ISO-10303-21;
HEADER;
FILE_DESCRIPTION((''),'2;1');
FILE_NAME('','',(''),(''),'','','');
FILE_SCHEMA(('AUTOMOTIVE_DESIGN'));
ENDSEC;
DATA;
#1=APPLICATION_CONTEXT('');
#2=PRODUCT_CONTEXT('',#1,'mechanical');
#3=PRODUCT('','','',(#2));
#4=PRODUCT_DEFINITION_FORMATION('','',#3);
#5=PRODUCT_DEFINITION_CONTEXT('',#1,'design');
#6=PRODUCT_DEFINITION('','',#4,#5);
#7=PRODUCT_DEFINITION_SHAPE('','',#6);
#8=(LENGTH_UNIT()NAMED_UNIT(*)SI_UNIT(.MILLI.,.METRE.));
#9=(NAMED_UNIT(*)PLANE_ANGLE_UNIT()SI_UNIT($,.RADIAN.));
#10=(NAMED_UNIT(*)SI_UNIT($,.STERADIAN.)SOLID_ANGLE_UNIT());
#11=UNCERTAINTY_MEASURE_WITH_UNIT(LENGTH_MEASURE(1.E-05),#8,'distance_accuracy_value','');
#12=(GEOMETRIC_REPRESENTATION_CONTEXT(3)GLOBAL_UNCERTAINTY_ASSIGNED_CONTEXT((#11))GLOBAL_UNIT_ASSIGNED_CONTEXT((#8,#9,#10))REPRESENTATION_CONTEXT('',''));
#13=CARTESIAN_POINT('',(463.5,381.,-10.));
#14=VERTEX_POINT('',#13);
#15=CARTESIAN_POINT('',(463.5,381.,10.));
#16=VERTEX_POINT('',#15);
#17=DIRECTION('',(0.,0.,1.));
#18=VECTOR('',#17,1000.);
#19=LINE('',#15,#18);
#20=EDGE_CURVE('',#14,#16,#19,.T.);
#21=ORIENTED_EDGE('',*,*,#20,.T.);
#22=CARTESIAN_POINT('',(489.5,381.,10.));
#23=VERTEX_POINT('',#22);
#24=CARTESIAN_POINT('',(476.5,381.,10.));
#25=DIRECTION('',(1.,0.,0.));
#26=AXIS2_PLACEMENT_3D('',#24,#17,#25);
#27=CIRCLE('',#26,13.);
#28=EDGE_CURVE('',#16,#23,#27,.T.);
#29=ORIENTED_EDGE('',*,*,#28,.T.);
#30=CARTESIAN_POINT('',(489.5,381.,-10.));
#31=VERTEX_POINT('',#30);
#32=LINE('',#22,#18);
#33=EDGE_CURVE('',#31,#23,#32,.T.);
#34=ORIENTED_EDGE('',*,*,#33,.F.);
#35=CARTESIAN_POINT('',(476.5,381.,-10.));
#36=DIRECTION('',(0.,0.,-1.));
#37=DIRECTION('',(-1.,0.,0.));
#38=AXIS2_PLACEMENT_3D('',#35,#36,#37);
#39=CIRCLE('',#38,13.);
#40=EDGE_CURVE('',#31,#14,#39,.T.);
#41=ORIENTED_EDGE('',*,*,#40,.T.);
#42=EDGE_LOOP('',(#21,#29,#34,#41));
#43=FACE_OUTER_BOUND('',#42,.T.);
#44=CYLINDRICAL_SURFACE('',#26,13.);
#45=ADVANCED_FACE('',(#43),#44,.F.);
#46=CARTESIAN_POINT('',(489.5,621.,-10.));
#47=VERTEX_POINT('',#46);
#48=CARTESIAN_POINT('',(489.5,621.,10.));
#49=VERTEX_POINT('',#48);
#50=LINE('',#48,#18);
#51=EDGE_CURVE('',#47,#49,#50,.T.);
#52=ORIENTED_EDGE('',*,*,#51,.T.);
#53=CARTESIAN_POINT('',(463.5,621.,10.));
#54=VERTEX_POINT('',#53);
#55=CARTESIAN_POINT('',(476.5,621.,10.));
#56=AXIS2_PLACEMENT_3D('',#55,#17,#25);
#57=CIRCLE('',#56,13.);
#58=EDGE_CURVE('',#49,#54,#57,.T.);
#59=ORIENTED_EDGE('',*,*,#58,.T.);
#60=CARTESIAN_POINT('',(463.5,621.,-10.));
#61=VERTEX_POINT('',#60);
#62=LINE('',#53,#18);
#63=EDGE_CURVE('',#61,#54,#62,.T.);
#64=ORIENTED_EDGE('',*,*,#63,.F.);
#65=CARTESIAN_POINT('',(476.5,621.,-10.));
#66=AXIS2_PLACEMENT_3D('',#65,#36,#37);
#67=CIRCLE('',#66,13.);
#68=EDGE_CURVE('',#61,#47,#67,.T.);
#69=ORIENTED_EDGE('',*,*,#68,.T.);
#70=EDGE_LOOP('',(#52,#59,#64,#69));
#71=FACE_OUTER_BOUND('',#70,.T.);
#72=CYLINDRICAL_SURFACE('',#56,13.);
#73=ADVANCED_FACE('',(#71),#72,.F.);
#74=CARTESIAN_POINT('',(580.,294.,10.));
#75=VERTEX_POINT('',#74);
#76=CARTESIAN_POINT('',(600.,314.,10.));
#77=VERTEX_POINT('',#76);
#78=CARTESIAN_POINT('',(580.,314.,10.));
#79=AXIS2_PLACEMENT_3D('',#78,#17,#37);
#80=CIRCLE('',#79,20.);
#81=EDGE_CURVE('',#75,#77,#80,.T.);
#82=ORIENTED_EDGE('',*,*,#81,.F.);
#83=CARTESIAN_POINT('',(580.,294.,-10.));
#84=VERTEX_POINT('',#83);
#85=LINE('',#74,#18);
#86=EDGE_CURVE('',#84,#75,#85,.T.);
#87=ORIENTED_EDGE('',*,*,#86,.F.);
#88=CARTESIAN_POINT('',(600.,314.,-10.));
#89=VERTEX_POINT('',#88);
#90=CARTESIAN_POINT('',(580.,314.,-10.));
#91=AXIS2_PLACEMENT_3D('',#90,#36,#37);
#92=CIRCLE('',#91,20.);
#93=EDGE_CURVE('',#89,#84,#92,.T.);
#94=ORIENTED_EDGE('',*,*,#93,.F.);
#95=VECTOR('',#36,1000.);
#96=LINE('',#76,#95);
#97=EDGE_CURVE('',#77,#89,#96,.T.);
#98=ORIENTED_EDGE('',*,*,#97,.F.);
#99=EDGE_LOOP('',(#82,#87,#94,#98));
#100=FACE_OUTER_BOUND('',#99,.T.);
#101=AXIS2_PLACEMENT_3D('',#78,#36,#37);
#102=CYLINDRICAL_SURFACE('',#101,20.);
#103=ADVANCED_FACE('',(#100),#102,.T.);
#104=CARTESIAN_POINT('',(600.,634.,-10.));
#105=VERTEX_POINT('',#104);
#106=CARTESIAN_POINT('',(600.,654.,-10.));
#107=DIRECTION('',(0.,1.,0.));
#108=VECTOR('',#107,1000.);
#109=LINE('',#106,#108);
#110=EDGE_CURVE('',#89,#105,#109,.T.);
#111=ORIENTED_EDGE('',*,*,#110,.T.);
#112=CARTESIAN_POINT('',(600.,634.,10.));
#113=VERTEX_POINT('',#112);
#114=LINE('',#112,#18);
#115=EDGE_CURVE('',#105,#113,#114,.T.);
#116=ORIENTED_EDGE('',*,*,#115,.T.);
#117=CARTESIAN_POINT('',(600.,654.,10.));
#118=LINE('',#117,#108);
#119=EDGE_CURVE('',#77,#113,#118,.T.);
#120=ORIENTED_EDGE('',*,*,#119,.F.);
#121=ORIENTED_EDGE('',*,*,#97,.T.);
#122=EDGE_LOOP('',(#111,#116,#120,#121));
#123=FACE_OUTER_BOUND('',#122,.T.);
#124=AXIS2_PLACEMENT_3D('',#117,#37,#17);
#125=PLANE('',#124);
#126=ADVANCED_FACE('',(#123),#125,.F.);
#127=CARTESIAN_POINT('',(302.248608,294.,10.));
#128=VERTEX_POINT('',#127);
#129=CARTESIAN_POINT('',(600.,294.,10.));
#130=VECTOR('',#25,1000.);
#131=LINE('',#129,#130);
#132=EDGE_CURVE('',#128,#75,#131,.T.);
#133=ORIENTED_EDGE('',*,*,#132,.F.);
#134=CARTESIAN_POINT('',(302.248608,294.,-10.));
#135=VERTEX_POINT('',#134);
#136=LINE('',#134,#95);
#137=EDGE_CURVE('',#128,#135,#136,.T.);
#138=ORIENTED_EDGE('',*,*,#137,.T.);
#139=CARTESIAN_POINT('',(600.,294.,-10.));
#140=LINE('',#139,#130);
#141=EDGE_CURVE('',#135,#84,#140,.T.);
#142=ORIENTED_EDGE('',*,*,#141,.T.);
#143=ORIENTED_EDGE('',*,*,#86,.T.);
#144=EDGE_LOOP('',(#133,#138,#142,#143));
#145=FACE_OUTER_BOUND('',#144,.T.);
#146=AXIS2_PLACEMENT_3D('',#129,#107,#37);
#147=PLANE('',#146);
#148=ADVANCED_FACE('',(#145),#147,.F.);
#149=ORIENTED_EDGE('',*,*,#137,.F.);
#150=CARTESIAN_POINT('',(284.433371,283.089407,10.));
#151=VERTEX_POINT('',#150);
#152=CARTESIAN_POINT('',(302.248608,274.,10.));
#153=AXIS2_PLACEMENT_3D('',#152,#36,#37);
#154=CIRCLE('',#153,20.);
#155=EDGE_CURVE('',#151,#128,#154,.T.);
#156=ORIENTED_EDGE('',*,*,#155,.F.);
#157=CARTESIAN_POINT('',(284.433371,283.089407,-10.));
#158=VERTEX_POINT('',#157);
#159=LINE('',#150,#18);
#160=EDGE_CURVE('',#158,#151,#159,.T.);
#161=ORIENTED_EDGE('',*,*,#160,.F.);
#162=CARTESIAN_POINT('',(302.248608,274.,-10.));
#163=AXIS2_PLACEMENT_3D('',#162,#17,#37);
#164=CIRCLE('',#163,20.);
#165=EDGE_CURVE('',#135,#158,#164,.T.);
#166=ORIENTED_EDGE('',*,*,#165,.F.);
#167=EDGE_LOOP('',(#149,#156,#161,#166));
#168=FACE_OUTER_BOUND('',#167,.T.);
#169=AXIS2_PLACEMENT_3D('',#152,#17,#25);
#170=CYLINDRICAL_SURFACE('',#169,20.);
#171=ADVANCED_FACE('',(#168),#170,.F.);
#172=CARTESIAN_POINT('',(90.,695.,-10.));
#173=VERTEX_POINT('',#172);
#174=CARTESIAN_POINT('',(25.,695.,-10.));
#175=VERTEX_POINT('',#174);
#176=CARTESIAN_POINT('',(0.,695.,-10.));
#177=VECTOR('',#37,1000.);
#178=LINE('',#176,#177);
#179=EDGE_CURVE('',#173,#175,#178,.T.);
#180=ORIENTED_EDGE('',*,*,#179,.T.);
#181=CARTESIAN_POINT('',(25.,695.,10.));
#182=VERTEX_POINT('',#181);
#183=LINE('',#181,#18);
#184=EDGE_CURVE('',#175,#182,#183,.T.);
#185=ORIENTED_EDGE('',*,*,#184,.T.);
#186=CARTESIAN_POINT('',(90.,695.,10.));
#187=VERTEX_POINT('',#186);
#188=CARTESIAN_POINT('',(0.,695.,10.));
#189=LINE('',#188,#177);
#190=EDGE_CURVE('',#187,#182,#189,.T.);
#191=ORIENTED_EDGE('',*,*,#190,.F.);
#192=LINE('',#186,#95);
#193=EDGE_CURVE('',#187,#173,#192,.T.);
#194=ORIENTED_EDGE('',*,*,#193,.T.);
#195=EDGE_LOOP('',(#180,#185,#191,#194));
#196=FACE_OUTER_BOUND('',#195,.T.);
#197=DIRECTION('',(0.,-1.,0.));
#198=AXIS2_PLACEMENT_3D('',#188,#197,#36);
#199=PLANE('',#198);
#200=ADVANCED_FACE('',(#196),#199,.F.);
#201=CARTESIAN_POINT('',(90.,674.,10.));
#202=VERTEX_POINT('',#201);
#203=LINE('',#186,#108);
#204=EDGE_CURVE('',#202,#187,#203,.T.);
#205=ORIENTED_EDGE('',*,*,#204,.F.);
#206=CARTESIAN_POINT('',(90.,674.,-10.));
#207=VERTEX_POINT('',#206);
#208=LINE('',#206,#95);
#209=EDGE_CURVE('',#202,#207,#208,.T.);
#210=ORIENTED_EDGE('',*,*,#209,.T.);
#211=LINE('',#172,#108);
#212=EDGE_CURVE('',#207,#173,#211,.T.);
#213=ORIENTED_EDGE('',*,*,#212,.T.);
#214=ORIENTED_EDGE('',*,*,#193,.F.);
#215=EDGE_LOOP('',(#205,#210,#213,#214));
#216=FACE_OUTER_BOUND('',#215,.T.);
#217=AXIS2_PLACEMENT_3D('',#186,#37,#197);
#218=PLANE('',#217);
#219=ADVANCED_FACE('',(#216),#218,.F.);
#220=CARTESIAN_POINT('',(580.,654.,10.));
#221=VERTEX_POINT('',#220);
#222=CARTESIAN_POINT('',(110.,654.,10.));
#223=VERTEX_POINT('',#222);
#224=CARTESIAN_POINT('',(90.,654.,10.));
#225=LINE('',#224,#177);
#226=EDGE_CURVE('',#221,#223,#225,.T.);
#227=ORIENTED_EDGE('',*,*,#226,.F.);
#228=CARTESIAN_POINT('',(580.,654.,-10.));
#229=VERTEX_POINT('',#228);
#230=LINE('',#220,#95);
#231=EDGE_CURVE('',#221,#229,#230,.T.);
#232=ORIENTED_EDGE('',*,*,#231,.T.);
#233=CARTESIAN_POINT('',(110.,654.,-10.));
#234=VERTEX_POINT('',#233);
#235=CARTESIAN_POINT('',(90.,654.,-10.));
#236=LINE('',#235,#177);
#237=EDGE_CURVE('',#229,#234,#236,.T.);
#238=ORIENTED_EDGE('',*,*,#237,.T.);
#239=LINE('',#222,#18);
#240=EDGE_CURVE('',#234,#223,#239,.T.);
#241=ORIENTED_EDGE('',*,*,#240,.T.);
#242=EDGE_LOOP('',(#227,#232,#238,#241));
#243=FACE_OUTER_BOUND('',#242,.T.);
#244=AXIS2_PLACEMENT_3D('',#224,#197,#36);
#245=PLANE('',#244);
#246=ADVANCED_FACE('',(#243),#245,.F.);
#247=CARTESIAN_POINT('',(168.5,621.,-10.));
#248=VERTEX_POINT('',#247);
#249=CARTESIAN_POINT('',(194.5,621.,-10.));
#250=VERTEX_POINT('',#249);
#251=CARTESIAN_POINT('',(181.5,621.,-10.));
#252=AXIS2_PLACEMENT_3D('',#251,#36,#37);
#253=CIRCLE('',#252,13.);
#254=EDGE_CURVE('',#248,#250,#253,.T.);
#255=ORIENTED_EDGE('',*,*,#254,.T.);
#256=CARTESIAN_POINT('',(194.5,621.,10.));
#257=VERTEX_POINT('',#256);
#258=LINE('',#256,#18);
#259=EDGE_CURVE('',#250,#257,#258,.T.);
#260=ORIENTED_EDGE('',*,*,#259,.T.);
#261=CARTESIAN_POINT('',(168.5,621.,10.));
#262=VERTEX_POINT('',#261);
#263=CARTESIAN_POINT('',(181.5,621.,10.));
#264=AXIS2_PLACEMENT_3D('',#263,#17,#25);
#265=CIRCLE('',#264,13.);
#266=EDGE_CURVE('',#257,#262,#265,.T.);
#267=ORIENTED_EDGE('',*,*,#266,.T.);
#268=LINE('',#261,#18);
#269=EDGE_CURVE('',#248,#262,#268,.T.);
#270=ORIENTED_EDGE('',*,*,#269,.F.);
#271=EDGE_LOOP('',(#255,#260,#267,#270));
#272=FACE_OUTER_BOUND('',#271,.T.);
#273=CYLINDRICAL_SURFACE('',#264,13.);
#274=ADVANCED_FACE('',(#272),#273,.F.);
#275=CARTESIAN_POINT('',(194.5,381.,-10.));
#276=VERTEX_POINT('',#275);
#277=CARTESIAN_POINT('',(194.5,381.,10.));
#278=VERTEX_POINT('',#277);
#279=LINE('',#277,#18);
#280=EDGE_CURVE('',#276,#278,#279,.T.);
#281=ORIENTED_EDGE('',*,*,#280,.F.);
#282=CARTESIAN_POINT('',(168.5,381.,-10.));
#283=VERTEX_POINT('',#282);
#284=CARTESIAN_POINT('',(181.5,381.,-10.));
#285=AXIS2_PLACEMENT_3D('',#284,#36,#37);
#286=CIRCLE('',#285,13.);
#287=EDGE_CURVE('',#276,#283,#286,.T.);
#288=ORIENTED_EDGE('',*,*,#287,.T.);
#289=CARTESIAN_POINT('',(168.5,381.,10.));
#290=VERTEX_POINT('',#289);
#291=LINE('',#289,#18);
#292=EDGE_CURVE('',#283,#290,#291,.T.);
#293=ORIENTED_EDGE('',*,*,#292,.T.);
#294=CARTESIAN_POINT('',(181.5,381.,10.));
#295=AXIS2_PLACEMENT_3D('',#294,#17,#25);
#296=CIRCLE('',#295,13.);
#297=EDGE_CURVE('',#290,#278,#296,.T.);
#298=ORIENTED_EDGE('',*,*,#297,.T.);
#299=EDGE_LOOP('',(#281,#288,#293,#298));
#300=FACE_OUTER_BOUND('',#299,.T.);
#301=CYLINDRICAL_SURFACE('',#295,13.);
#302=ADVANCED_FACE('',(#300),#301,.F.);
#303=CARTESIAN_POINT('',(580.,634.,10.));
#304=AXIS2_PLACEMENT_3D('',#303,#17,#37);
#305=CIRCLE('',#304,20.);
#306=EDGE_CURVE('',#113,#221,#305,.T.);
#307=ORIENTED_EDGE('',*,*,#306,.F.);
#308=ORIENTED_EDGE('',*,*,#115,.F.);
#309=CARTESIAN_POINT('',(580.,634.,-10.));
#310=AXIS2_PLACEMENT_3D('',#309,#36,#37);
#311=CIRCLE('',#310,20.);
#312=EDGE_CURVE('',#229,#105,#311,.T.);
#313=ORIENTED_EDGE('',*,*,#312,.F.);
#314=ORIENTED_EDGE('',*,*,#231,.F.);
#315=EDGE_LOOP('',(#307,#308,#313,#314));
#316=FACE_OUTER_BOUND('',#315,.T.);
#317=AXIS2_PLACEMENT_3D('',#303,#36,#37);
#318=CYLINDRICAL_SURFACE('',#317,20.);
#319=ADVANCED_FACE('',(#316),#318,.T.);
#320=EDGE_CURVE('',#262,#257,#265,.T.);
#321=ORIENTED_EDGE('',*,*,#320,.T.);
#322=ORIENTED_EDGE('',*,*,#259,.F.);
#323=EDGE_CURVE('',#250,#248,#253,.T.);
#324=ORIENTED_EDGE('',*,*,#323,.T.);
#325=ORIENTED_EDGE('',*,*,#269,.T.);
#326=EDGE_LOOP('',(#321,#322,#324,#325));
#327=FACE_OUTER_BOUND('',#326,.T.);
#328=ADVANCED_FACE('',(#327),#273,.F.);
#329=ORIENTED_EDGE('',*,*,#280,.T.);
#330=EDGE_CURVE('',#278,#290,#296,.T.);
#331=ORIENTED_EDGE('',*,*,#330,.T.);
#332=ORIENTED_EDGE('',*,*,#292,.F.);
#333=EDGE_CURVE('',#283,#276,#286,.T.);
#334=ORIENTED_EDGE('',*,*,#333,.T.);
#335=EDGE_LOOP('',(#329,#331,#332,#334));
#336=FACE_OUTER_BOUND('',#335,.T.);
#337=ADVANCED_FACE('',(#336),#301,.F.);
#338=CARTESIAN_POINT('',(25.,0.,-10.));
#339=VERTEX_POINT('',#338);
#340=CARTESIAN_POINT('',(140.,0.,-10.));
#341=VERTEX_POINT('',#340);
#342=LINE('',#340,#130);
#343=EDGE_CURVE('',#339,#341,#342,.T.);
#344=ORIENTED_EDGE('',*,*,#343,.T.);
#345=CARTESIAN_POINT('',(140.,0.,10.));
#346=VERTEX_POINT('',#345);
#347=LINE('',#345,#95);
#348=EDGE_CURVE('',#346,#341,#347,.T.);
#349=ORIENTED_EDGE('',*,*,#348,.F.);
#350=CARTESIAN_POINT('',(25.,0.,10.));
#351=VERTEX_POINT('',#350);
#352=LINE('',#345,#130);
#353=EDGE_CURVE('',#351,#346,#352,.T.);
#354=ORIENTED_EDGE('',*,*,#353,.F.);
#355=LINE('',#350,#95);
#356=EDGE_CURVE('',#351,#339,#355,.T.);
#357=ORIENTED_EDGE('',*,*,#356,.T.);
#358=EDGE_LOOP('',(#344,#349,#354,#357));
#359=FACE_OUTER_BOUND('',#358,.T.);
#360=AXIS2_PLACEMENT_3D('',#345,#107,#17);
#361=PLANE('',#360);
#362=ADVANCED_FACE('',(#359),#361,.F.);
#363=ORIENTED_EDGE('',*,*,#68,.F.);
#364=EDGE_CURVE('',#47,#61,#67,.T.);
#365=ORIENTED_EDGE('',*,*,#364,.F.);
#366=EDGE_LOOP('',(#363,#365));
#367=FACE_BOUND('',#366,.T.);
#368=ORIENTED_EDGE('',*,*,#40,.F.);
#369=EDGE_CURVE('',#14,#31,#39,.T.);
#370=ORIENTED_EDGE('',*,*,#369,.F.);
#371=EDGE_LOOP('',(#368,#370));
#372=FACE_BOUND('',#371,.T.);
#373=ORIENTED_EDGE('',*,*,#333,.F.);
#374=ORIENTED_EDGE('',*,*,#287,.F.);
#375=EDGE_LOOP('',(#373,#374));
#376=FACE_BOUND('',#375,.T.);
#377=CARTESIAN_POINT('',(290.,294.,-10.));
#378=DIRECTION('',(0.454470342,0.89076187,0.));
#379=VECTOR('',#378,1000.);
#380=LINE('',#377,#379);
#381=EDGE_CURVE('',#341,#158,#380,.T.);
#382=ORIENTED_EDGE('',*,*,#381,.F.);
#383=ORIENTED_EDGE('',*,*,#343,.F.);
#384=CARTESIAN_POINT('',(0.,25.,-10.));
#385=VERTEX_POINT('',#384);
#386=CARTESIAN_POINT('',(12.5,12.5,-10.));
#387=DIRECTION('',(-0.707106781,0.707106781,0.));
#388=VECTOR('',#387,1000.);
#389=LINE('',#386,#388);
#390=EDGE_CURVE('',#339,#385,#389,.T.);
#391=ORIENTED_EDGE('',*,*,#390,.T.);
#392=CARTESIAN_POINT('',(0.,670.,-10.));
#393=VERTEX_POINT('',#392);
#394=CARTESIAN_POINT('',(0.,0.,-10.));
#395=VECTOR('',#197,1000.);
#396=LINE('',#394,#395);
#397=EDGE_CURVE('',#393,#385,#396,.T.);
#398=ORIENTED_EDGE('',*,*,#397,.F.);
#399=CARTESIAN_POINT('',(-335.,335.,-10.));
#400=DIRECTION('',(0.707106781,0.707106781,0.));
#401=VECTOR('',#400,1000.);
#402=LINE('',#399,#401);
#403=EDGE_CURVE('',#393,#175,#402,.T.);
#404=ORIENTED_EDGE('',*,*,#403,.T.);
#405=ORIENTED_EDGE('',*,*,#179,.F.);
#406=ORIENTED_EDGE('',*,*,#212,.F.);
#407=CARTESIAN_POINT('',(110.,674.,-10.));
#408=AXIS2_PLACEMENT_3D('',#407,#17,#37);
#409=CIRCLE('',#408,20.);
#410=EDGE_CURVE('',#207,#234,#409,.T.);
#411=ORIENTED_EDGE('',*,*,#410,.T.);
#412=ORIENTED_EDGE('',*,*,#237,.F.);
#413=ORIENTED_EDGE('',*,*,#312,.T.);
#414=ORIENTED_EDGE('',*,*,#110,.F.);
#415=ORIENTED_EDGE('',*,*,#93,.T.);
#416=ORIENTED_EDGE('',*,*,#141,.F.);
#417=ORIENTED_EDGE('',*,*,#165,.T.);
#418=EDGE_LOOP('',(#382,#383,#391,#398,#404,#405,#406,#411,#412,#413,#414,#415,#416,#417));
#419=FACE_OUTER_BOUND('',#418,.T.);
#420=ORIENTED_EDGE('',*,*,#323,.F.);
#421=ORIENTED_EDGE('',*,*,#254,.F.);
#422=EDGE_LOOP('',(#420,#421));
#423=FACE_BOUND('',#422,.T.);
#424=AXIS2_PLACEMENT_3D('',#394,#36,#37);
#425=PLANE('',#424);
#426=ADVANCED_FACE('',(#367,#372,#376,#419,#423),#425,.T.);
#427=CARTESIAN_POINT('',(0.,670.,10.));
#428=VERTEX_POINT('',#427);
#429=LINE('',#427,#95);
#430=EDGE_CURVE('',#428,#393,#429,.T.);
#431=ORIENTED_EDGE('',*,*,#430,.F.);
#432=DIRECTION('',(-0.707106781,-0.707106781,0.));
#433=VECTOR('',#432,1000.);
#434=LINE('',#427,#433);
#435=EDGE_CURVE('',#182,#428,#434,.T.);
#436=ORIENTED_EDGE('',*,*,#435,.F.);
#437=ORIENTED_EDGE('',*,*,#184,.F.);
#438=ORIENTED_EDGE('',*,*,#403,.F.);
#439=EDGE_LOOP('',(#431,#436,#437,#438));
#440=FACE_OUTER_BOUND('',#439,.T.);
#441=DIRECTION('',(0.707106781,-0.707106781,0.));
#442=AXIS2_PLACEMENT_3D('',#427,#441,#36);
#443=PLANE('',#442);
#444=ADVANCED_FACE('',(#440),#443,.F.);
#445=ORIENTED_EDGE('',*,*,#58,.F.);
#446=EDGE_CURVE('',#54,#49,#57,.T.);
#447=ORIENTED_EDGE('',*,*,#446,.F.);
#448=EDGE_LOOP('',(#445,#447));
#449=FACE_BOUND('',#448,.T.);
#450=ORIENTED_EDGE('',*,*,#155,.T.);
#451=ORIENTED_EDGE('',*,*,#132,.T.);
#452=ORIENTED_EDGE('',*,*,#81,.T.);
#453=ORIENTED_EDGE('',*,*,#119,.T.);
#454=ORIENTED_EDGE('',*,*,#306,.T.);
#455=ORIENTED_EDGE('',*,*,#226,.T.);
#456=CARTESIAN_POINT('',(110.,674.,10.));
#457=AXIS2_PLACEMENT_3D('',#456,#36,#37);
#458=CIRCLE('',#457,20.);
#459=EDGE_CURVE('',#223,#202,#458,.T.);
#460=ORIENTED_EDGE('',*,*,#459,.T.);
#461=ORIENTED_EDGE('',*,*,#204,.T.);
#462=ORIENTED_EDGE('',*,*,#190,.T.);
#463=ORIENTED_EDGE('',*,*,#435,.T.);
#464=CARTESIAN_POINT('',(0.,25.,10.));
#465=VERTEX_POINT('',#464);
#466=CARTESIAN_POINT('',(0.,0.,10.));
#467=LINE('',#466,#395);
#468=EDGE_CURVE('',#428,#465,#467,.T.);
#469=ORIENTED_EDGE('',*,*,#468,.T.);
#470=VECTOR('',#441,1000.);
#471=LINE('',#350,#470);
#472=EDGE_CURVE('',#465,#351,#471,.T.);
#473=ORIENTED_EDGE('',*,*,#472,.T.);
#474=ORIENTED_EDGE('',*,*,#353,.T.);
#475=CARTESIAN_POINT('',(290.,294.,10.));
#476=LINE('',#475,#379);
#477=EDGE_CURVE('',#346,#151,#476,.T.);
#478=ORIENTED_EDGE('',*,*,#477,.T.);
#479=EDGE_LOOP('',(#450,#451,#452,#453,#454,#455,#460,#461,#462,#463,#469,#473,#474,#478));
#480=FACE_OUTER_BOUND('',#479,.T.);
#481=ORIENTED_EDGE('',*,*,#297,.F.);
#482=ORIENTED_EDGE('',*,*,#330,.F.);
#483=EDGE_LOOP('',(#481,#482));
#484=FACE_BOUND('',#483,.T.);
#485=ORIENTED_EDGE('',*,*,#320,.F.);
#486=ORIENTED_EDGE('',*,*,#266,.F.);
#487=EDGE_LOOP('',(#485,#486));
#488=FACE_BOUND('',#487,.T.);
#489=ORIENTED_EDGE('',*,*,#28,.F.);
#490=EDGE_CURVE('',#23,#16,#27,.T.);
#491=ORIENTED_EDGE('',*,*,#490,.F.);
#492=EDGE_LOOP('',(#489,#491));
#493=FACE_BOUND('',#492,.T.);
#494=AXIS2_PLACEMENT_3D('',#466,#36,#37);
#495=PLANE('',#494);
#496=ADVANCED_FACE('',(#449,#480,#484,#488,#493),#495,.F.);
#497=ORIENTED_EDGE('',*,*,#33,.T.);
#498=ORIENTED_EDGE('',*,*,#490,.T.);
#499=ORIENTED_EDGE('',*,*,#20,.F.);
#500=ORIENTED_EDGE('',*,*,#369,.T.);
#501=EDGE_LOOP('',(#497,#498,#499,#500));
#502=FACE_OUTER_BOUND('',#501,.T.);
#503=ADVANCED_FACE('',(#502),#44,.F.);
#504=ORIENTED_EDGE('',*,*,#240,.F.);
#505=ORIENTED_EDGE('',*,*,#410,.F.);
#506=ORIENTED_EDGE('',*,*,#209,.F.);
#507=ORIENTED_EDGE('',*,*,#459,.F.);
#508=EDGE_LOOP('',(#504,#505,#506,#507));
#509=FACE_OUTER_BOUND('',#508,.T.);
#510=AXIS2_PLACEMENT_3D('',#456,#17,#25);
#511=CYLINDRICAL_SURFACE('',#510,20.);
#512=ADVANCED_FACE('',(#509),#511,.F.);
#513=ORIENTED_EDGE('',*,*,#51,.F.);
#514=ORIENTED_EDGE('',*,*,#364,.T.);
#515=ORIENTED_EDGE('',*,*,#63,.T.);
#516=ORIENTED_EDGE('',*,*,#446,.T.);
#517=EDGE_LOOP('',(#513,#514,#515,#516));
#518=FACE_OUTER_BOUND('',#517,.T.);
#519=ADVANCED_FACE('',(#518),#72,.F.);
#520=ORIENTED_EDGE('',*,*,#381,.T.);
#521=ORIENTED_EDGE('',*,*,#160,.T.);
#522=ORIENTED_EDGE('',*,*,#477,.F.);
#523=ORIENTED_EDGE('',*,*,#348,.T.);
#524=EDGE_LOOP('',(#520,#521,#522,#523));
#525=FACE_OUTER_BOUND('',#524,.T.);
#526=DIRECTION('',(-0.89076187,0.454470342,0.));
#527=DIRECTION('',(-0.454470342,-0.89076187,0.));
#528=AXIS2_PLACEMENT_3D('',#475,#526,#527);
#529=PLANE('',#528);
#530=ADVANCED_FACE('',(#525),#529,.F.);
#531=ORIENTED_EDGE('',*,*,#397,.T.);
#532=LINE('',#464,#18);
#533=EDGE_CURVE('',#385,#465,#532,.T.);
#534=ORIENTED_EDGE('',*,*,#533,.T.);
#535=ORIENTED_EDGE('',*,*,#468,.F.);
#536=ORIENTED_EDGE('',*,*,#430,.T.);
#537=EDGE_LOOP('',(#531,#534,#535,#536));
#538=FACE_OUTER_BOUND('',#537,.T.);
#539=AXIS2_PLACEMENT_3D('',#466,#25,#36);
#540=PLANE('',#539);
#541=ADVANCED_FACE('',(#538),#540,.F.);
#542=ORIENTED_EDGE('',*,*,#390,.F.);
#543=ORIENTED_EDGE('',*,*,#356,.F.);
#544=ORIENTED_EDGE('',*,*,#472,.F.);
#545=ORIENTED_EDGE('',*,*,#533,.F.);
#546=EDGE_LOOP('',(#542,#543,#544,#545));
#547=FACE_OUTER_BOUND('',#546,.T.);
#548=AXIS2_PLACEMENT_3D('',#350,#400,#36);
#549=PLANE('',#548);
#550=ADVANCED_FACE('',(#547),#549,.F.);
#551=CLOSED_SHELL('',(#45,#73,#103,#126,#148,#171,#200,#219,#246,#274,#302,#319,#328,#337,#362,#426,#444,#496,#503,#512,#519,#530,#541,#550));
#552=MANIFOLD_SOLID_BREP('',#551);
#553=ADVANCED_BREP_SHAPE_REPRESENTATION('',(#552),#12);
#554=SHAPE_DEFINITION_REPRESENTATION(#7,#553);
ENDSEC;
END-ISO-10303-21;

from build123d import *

# Parameters (mm, degrees)
BOSS_EXTRUDE1_DEPTH   = 10
CHAMFER1_SIZE         = 25
FILLET1_R             = 20
F_26_DIAMETER_HOLE1_D = 26


with BuildPart() as part:
    # Sketch1 → Boss-Extrude1 (new, symmetric)
    with BuildSketch(Plane.XY):
        Polygon((0, 0), (0, 695), (90, 695), (90, 654), (600, 654), (600, 294), (290, 294), (140, 0), align=None)
    extrude(amount=BOSS_EXTRUDE1_DEPTH, both=True)

    # Chamfer1
    chamfer1_edges = [part.edges().sort_by_distance(p)[0] for p in [
        (0, 0, 0),
        (0, 695, 0),
    ]]
    chamfer(chamfer1_edges, length=CHAMFER1_SIZE)

    # Fillet1
    fillet1_edges = [part.edges().sort_by_distance(p)[0] for p in [
        (90, 654, 0),
        (600, 654, 0),
        (600, 294, 0),
        (290, 294, 0),
    ]]
    fillet(fillet1_edges, radius=FILLET1_R)

    # Ø26 Diameter Hole1 (through all)
    with Locations(Plane.XY.offset(10)):
        with Locations((181.5, 621), (476.5, 621), (476.5, 381), (181.5, 381)):
            Hole(F_26_DIAMETER_HOLE1_D / 2)


solid = part.part
